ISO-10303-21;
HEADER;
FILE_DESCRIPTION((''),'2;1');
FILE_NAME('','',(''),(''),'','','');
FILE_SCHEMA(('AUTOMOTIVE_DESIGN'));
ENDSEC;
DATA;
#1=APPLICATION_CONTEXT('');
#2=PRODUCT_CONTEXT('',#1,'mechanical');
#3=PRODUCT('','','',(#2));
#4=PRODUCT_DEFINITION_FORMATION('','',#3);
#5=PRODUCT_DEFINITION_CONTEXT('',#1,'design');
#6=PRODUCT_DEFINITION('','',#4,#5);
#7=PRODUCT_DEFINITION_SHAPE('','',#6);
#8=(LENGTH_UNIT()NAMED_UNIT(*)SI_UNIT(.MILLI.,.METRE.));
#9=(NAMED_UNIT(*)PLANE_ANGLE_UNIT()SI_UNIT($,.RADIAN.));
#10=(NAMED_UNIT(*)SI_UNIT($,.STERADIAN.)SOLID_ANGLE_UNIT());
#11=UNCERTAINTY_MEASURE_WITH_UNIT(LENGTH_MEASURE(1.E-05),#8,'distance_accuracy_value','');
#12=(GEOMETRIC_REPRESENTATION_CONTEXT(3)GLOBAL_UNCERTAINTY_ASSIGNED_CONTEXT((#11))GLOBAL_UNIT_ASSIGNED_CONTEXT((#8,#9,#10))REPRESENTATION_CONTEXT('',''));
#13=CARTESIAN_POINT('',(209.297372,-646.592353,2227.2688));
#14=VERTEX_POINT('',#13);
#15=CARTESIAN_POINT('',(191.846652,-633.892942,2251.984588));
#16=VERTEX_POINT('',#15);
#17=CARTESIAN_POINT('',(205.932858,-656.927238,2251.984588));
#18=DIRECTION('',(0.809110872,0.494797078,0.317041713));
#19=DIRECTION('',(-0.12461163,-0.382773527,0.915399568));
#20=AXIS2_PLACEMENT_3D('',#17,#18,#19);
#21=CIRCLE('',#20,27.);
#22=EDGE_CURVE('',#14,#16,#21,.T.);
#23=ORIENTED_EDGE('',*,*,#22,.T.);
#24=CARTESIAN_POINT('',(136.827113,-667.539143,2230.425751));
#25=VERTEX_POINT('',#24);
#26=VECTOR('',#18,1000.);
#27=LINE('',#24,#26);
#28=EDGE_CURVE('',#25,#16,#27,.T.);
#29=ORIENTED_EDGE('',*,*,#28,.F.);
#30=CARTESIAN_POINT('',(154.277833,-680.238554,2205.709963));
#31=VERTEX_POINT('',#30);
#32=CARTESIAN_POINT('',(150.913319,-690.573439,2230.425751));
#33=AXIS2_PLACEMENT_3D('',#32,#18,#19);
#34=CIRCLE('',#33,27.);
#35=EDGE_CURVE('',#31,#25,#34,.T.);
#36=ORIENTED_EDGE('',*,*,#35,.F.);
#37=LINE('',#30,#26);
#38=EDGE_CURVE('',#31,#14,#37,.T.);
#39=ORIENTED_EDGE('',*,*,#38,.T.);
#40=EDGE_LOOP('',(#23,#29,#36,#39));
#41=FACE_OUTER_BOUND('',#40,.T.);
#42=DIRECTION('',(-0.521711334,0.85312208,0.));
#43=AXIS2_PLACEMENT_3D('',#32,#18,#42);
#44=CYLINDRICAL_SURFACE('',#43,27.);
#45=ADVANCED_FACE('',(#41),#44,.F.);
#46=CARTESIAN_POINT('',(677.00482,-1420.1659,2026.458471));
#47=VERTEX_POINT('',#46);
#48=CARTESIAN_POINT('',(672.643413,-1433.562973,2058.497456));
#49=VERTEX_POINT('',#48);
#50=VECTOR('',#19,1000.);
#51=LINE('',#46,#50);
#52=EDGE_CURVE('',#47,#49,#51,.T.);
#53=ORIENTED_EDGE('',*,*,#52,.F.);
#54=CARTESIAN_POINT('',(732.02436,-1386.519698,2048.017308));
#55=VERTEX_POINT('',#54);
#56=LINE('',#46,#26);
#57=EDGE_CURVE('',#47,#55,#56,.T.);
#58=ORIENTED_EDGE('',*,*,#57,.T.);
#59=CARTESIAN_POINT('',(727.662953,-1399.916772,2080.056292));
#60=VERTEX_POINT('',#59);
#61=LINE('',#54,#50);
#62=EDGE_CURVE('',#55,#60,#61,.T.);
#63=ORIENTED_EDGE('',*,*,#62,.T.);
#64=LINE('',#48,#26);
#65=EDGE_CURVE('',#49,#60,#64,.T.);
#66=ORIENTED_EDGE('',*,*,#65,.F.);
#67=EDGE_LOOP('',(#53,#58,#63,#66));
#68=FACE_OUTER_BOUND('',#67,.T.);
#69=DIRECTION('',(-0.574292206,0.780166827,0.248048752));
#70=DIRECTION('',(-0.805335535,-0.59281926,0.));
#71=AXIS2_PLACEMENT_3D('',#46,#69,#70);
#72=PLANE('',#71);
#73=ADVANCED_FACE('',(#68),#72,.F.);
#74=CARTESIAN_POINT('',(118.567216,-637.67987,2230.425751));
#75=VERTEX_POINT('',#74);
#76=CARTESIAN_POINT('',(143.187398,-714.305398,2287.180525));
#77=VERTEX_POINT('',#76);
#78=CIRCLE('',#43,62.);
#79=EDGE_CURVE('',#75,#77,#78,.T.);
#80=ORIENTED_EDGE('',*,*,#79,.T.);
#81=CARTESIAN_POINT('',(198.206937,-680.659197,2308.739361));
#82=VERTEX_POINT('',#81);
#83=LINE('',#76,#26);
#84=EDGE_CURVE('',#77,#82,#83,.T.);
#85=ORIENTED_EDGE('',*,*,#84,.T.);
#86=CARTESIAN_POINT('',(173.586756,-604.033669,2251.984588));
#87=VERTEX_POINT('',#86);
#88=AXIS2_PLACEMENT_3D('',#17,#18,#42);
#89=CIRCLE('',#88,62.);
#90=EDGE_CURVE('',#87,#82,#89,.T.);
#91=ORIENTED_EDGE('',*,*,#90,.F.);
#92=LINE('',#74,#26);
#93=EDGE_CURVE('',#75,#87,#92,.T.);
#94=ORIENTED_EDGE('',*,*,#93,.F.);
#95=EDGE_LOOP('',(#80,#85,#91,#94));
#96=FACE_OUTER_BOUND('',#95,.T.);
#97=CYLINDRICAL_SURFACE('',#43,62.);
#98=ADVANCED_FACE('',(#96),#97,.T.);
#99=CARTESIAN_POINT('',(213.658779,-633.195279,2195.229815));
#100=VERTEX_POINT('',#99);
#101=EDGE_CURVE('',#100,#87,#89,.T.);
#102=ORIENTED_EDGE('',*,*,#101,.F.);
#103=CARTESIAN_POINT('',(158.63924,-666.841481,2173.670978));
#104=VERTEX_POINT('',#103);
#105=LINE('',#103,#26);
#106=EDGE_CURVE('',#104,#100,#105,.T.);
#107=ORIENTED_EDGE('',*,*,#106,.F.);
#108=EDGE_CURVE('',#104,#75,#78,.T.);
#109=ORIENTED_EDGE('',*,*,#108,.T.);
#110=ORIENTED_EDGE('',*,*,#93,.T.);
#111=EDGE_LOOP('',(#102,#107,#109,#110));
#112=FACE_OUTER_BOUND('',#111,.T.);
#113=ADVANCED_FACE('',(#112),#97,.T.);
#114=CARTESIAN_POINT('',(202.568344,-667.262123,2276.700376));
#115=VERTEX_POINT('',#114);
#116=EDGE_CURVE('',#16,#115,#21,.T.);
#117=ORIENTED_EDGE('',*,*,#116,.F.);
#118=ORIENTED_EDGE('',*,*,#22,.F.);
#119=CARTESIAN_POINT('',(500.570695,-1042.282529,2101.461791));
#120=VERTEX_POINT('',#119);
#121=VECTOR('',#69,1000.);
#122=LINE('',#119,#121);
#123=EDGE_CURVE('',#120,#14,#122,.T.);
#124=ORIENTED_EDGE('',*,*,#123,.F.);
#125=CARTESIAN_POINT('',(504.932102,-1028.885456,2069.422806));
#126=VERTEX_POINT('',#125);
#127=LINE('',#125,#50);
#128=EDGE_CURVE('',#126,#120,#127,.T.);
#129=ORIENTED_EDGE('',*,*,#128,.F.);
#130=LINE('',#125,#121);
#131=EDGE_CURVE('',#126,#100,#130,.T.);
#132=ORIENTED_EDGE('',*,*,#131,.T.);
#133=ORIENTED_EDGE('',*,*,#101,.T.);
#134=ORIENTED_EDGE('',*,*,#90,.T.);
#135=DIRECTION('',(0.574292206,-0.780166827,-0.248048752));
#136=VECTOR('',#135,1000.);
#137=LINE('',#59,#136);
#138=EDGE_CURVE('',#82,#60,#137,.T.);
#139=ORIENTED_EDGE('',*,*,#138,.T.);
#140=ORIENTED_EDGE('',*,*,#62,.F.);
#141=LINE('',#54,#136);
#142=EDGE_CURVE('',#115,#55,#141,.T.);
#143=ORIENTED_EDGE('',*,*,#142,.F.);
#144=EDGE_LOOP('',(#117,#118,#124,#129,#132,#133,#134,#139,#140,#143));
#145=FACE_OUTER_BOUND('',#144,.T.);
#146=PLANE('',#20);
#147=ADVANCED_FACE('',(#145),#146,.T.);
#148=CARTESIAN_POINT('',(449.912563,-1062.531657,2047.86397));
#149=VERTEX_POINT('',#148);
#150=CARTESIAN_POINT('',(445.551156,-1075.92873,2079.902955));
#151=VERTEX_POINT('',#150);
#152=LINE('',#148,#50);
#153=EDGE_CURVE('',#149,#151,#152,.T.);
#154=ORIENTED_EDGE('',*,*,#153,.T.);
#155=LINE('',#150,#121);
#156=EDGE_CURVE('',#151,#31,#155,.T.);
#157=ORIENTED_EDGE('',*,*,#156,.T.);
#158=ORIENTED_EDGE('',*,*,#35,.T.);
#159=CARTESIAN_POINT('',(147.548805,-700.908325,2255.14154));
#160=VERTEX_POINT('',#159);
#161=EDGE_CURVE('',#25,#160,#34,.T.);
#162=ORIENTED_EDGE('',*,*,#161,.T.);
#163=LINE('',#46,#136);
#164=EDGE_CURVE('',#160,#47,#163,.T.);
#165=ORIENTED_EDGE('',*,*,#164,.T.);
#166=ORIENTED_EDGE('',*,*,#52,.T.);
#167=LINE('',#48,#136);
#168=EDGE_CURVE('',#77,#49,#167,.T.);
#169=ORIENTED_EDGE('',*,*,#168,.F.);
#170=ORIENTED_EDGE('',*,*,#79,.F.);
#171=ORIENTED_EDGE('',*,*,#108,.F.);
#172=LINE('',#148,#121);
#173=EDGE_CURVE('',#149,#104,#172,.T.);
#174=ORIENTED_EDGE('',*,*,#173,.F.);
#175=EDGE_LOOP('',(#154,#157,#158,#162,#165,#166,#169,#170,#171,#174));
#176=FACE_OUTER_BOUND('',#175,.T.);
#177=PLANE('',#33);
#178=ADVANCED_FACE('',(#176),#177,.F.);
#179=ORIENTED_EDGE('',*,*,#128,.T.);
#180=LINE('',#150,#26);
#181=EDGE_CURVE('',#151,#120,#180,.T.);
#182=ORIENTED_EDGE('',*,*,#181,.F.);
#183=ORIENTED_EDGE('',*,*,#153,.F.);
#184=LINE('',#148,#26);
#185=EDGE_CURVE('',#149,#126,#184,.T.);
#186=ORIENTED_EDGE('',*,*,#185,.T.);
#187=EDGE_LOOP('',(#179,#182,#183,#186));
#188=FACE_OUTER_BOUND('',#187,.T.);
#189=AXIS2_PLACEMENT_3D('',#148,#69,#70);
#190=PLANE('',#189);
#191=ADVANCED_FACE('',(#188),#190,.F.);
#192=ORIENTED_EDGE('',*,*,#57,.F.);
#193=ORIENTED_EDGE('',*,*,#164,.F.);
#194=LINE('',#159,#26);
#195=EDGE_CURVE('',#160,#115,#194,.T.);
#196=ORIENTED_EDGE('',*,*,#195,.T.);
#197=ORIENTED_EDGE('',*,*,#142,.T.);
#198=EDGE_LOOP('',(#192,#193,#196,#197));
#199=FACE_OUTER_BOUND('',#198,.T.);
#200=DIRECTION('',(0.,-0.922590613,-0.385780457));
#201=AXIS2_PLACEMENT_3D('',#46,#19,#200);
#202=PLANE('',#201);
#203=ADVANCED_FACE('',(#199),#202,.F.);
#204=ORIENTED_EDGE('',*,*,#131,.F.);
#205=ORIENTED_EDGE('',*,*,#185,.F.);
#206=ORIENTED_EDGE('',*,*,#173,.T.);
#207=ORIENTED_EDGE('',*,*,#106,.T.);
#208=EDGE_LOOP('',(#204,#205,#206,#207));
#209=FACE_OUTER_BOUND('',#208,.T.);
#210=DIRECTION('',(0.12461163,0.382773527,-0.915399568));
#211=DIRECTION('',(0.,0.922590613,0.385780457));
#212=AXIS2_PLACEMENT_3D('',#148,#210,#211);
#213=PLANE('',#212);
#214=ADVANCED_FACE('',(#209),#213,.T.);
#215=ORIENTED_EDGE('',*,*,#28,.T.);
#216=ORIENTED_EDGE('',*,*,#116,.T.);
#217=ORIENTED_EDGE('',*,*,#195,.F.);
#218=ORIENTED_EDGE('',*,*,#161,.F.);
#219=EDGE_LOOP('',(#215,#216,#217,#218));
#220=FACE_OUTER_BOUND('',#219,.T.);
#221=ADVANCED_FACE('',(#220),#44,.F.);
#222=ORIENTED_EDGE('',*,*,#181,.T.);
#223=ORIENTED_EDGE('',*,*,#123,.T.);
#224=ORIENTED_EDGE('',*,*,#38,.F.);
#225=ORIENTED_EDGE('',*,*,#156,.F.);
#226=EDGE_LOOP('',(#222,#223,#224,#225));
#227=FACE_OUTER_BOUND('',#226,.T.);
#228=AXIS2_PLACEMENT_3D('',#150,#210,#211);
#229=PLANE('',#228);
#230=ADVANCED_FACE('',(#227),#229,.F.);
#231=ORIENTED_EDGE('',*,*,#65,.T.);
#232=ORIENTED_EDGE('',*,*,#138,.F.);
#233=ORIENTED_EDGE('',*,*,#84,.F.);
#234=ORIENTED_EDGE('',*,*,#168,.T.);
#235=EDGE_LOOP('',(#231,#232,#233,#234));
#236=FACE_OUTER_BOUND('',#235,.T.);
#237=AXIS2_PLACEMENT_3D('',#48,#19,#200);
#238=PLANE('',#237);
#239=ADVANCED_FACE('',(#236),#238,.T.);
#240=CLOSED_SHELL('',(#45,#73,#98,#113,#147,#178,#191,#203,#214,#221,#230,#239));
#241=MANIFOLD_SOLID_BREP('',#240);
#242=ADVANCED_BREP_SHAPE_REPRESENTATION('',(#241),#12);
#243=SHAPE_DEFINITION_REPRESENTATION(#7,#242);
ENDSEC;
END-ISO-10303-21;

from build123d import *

# Parameters (mm, degrees)
EXTRUDE_1_DEPTH = 34


with BuildPart() as part:
    # 草图2 → 拉伸-薄壁1 (new, symmetric)
    with BuildSketch(Plane(origin=(290.969985959, -860.871008049, 2246.011610274), x_dir=(-0.12461162955889699, -0.382773527459934, 0.9153995676504089), z_dir=(0.8091108722091485, 0.49479707812616053, 0.3170417132661968))):
        with BuildLine():
            Line((0, 712.5), (0, -209.427913233))
            ThreePointArc((0, -209.427913233), (-62, -271.427913233), (-124, -209.427913233))
            Line((-124, -209.427913233), (-124, 297.758706857))
            Line((-124, 297.758706857), (-89, 297.758706857))
            Line((-89, 297.758706857), (-89, -209.427913233))
            ThreePointArc((-89, -209.427913233), (-62, -236.427913233), (-35, -209.427913233))
            Line((-35, -209.427913233), (-35, 712.5))
            Line((-35, 712.5), (0, 712.5))
        make_face()
    extrude(amount=EXTRUDE_1_DEPTH, both=True)


solid = part.part
